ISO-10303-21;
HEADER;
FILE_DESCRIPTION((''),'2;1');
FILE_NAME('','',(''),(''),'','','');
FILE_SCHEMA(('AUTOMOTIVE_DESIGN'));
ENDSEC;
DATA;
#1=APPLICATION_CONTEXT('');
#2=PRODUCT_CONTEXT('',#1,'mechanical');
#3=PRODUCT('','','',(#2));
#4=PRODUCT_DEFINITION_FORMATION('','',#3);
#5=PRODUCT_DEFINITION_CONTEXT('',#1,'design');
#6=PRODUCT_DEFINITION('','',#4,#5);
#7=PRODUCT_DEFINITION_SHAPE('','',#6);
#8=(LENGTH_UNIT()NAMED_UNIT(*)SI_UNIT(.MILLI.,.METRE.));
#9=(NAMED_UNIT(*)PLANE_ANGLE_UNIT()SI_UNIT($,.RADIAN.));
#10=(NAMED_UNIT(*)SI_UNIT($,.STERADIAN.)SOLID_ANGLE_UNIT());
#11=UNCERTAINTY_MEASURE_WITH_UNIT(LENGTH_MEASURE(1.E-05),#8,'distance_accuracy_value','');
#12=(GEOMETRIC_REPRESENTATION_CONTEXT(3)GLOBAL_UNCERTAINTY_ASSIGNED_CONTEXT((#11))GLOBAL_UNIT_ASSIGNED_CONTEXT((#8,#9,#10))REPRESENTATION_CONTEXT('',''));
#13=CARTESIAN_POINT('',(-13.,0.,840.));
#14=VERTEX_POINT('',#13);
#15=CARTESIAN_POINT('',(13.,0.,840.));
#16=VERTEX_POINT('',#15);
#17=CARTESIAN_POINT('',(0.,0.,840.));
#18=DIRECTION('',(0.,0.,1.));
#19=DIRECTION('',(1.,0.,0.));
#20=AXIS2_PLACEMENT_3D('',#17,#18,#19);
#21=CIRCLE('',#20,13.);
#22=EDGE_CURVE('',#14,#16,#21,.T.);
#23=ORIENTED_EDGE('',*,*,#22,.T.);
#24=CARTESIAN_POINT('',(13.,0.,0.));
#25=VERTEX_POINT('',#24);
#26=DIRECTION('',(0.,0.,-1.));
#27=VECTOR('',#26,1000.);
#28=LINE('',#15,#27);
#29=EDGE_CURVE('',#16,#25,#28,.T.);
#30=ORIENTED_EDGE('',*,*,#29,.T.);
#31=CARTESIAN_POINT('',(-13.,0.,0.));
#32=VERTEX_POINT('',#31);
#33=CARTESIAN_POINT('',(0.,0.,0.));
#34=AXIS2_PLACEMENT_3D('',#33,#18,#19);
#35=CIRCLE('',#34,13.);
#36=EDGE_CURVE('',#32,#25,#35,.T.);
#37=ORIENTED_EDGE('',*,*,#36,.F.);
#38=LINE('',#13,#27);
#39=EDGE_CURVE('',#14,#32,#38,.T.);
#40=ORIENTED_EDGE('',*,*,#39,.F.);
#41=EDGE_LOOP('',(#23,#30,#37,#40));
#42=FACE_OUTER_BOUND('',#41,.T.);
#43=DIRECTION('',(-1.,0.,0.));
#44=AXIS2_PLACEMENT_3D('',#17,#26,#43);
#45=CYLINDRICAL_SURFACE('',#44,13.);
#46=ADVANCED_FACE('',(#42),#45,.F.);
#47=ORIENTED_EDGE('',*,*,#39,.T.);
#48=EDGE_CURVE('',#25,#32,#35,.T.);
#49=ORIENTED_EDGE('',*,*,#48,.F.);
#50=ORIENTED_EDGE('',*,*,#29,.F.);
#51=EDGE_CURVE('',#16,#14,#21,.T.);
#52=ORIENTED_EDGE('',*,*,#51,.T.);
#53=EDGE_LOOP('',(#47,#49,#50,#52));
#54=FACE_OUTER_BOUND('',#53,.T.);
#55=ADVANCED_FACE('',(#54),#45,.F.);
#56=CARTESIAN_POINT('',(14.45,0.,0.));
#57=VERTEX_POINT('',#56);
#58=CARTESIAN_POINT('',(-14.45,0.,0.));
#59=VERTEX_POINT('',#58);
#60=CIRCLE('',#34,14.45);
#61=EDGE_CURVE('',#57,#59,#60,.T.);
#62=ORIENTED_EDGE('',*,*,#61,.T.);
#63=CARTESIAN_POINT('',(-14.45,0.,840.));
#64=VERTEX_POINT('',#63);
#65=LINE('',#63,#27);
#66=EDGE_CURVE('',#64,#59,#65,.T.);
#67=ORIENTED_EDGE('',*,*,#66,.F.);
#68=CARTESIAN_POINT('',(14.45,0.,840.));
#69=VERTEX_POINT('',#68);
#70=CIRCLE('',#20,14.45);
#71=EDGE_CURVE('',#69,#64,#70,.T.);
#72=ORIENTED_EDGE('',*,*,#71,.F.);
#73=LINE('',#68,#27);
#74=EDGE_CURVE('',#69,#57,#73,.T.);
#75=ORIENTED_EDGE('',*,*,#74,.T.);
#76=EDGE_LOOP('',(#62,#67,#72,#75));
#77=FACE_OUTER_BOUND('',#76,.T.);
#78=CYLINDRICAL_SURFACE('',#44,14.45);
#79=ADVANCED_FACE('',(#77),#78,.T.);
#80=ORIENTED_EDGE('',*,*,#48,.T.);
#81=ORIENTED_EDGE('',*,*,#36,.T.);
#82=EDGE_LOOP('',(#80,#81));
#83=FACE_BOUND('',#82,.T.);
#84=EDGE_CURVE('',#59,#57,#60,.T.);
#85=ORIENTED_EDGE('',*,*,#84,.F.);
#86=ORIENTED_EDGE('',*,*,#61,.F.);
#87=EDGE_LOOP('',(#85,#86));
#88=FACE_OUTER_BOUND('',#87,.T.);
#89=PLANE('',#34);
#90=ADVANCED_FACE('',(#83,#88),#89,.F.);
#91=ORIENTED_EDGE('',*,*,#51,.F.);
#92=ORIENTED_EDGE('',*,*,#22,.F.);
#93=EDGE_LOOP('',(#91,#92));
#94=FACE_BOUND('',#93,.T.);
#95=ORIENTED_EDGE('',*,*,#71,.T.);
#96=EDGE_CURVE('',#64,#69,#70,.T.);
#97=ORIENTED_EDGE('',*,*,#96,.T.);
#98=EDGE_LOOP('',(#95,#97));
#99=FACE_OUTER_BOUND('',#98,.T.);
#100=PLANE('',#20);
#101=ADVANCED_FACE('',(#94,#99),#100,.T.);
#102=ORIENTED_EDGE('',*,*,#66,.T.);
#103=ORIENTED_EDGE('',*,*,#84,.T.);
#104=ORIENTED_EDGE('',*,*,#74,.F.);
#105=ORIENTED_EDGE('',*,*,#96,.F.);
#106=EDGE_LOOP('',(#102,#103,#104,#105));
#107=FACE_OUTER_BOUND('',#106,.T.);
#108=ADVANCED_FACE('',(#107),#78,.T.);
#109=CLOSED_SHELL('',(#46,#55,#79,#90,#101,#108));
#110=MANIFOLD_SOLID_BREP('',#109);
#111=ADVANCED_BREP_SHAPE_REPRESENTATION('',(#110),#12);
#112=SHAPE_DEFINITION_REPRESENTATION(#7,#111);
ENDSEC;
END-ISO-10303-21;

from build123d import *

# Parameters (mm, degrees)
SKETCH1_R           = 14.45
SKETCH1_R_2         = 13
BOSS_EXTRUDE1_DEPTH = 840


with BuildPart() as part:
    # Sketch1 → Boss-Extrude1 (new body)
    with BuildSketch(Plane.XY):
        Circle(SKETCH1_R)
        Circle(SKETCH1_R_2, mode=Mode.SUBTRACT)
    extrude(amount=BOSS_EXTRUDE1_DEPTH)


solid = part.part
